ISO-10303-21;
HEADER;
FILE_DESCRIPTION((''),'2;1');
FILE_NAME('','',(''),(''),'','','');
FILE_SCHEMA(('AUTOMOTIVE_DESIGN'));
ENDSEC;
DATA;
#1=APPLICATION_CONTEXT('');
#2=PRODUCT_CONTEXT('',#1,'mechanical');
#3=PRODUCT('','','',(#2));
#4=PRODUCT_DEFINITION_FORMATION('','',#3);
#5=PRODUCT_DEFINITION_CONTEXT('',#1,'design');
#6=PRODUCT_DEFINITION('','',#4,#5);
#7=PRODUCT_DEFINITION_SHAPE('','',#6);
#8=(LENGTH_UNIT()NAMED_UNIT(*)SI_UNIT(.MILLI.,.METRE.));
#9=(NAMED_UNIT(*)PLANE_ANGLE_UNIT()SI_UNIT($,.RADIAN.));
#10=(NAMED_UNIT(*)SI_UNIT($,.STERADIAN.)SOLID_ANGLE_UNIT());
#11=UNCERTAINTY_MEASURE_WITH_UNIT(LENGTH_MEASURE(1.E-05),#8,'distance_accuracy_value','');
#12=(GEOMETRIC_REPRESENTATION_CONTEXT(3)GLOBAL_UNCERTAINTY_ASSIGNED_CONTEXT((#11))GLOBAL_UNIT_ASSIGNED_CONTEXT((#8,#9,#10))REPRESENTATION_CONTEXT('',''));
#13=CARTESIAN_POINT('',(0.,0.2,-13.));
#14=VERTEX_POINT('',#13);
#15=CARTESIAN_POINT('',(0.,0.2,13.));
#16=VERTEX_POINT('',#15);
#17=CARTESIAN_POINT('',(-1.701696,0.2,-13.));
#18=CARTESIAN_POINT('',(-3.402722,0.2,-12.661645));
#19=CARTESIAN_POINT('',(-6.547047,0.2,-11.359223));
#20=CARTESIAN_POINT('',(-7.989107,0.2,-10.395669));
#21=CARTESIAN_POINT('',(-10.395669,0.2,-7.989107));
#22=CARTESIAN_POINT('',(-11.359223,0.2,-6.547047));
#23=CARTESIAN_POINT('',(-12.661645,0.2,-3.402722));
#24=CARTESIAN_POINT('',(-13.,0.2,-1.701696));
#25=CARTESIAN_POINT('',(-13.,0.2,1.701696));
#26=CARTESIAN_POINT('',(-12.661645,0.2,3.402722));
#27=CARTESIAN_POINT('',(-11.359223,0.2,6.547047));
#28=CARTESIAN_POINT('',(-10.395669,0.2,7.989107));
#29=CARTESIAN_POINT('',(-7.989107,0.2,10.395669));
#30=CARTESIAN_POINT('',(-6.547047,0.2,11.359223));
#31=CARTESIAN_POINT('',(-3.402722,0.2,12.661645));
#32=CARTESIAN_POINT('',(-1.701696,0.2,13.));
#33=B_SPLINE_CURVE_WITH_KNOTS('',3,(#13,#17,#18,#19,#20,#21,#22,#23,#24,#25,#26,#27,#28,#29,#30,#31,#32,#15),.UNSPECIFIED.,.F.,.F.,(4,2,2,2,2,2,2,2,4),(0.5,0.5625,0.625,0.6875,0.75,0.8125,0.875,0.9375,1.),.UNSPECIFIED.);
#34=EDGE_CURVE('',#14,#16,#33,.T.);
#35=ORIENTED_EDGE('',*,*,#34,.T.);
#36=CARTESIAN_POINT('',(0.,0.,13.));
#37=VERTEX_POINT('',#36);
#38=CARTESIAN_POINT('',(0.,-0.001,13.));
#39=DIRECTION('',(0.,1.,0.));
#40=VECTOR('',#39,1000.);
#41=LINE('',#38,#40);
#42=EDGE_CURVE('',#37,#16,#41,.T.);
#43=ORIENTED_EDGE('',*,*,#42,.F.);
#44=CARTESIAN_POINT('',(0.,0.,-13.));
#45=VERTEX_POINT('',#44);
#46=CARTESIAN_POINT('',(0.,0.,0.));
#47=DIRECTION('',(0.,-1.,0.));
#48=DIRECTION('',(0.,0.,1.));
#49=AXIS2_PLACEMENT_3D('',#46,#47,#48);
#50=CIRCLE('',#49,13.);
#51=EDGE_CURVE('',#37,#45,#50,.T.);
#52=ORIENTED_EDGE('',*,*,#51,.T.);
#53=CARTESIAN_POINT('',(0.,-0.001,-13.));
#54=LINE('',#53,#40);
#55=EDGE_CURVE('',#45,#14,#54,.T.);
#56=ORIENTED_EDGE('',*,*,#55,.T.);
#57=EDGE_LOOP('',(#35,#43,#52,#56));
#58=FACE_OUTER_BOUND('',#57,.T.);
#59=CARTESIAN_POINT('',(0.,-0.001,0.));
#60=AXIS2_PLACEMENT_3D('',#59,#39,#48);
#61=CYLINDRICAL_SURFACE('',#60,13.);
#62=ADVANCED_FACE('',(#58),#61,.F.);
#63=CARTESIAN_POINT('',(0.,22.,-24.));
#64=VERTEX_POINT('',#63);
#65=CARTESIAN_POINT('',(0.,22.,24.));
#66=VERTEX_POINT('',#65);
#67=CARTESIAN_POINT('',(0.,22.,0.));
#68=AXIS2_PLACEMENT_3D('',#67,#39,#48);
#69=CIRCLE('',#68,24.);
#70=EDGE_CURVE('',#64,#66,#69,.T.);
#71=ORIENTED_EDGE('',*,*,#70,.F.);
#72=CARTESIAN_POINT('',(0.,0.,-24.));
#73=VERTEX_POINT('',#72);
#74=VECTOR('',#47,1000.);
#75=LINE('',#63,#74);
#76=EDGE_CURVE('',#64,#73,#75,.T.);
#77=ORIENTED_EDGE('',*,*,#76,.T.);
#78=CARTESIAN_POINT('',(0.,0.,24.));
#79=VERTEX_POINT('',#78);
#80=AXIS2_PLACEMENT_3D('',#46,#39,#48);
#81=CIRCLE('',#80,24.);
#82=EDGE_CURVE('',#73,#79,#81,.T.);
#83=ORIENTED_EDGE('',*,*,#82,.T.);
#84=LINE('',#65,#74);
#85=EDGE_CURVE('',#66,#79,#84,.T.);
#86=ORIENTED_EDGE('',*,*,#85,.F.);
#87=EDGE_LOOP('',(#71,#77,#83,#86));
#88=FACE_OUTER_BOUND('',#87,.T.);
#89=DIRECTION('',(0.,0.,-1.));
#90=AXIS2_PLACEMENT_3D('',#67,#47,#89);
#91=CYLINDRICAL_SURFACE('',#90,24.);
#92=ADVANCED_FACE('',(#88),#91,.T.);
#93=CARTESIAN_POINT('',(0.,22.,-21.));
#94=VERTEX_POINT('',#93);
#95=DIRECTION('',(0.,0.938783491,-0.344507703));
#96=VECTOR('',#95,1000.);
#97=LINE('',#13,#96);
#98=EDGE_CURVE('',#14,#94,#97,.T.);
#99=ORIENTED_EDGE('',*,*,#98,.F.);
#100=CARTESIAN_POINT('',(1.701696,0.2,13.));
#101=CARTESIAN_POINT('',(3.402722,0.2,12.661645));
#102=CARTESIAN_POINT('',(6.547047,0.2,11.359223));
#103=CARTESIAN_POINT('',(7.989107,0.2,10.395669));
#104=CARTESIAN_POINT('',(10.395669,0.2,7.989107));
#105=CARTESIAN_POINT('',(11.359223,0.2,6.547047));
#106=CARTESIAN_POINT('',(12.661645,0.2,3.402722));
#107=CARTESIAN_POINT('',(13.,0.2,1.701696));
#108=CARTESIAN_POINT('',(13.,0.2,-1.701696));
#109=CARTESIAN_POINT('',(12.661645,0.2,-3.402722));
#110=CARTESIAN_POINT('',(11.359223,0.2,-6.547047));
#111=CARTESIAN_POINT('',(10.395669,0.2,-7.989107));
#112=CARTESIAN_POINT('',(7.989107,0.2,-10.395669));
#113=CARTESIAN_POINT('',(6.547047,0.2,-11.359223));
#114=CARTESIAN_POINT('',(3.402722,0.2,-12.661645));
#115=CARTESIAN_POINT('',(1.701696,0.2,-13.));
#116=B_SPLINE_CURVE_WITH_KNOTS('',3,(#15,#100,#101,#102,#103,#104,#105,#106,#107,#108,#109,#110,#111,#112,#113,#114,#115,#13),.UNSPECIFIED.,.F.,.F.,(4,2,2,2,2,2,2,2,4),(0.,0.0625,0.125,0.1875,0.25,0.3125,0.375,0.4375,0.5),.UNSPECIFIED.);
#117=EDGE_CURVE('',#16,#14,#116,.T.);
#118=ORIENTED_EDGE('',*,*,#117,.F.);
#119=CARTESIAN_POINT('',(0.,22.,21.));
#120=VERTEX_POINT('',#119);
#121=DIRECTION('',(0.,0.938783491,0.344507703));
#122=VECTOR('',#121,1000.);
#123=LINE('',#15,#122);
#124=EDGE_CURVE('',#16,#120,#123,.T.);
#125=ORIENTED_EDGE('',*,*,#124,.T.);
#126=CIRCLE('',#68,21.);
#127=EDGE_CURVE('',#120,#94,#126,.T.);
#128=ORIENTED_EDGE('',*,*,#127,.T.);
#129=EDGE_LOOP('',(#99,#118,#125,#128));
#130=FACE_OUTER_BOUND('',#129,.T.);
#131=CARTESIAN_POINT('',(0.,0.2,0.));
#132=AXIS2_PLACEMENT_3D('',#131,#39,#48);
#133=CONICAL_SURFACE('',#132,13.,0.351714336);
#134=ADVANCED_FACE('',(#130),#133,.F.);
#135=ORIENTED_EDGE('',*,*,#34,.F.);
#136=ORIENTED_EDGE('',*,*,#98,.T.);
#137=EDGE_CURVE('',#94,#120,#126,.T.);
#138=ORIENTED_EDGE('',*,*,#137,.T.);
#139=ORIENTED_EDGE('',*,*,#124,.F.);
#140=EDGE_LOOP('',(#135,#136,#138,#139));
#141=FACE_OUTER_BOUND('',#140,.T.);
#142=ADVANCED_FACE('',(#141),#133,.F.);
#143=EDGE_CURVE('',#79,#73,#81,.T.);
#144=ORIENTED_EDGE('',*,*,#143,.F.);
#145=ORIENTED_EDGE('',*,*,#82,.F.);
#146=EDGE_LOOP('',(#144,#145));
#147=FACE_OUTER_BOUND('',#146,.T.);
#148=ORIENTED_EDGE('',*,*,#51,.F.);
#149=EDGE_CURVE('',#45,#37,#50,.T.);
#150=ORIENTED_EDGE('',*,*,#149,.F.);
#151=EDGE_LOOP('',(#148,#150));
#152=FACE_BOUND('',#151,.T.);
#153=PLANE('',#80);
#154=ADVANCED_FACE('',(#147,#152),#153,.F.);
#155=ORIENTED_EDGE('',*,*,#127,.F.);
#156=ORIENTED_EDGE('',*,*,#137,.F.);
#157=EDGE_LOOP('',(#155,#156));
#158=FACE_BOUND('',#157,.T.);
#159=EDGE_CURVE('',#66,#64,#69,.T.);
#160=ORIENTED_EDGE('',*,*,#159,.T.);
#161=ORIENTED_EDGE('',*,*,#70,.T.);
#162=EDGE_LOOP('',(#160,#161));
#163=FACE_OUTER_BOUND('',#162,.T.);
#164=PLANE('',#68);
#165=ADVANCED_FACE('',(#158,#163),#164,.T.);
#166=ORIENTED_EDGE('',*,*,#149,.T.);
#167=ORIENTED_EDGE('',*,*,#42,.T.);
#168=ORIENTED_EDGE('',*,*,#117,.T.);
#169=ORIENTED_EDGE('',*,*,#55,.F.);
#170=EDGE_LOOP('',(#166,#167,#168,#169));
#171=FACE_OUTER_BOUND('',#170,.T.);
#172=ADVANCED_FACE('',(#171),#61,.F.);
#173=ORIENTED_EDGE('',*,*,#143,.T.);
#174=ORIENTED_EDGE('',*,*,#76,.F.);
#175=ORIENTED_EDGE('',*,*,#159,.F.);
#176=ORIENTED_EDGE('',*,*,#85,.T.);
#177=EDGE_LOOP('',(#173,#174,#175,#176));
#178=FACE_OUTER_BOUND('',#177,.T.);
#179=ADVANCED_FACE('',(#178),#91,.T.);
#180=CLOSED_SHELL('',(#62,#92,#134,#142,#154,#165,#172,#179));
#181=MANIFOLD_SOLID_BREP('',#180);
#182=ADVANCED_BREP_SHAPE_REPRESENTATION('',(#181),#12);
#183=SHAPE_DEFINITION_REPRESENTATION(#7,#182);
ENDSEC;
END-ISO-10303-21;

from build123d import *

# Parameters (mm, degrees)
RING_OUTLINE_SKETCH_48_R  = 24
RING_BODY_48X22_DEPTH     = 22
TAPER_TOP_PROFILE_40_R    = 21
TAPER_BOTTOM_PROFILE_20_R = 13
THROUGH_BORE_20_REACH     = 42.339
THROUGH_BORE_SKETCH_20_R  = 13


with BuildPart() as part:
    # Ring Outline Sketch Ø48 → Ring Body Ø48x22 (new body)
    with BuildSketch(Plane(origin=(0, 0, 0), x_dir=(1, 0, 0), z_dir=(0, 1, 0))):
        with Locations(Location((0, 0, 0), (0, 0, 270))):
            Circle(RING_OUTLINE_SKETCH_48_R)
    extrude(amount=RING_BODY_48X22_DEPTH)

    # Taper Top Profile Ø40 → Conical Bore Ø40-Ø20 section 0
    with BuildSketch(Plane(origin=(0, 22, 0), x_dir=(1, 0, 0), z_dir=(0, 1, 0))):
        Circle(TAPER_TOP_PROFILE_40_R)
    # Taper Bottom Profile Ø20 → Conical Bore Ø40-Ø20 section 1
    with BuildSketch(Plane(origin=(0, 0.2, 0), x_dir=(1, 0, 0), z_dir=(0, 1, 0))):
        Circle(TAPER_BOTTOM_PROFILE_20_R)
    loft(mode=Mode.SUBTRACT)

    # Through Bore Sketch Ø20 → Through Bore Ø20 (cut, up to next)
    with BuildSketch(Plane(origin=(0, 0.2, 0), x_dir=(1, 0, 0), z_dir=(0, 1, 0)), mode=Mode.PRIVATE) as through_bore_20_sk1:
        with Locations(Location((0, 0, 0), (0, 0, 270))):
            Circle(THROUGH_BORE_SKETCH_20_R)
    through_bore_20_tool1 = extrude(through_bore_20_sk1.sketch, amount=-THROUGH_BORE_20_REACH, mode=Mode.PRIVATE) & part.part
    add(through_bore_20_tool1.solids().sort_by_distance((0, 0.2, 0))[0], mode=Mode.SUBTRACT)


solid = part.part
